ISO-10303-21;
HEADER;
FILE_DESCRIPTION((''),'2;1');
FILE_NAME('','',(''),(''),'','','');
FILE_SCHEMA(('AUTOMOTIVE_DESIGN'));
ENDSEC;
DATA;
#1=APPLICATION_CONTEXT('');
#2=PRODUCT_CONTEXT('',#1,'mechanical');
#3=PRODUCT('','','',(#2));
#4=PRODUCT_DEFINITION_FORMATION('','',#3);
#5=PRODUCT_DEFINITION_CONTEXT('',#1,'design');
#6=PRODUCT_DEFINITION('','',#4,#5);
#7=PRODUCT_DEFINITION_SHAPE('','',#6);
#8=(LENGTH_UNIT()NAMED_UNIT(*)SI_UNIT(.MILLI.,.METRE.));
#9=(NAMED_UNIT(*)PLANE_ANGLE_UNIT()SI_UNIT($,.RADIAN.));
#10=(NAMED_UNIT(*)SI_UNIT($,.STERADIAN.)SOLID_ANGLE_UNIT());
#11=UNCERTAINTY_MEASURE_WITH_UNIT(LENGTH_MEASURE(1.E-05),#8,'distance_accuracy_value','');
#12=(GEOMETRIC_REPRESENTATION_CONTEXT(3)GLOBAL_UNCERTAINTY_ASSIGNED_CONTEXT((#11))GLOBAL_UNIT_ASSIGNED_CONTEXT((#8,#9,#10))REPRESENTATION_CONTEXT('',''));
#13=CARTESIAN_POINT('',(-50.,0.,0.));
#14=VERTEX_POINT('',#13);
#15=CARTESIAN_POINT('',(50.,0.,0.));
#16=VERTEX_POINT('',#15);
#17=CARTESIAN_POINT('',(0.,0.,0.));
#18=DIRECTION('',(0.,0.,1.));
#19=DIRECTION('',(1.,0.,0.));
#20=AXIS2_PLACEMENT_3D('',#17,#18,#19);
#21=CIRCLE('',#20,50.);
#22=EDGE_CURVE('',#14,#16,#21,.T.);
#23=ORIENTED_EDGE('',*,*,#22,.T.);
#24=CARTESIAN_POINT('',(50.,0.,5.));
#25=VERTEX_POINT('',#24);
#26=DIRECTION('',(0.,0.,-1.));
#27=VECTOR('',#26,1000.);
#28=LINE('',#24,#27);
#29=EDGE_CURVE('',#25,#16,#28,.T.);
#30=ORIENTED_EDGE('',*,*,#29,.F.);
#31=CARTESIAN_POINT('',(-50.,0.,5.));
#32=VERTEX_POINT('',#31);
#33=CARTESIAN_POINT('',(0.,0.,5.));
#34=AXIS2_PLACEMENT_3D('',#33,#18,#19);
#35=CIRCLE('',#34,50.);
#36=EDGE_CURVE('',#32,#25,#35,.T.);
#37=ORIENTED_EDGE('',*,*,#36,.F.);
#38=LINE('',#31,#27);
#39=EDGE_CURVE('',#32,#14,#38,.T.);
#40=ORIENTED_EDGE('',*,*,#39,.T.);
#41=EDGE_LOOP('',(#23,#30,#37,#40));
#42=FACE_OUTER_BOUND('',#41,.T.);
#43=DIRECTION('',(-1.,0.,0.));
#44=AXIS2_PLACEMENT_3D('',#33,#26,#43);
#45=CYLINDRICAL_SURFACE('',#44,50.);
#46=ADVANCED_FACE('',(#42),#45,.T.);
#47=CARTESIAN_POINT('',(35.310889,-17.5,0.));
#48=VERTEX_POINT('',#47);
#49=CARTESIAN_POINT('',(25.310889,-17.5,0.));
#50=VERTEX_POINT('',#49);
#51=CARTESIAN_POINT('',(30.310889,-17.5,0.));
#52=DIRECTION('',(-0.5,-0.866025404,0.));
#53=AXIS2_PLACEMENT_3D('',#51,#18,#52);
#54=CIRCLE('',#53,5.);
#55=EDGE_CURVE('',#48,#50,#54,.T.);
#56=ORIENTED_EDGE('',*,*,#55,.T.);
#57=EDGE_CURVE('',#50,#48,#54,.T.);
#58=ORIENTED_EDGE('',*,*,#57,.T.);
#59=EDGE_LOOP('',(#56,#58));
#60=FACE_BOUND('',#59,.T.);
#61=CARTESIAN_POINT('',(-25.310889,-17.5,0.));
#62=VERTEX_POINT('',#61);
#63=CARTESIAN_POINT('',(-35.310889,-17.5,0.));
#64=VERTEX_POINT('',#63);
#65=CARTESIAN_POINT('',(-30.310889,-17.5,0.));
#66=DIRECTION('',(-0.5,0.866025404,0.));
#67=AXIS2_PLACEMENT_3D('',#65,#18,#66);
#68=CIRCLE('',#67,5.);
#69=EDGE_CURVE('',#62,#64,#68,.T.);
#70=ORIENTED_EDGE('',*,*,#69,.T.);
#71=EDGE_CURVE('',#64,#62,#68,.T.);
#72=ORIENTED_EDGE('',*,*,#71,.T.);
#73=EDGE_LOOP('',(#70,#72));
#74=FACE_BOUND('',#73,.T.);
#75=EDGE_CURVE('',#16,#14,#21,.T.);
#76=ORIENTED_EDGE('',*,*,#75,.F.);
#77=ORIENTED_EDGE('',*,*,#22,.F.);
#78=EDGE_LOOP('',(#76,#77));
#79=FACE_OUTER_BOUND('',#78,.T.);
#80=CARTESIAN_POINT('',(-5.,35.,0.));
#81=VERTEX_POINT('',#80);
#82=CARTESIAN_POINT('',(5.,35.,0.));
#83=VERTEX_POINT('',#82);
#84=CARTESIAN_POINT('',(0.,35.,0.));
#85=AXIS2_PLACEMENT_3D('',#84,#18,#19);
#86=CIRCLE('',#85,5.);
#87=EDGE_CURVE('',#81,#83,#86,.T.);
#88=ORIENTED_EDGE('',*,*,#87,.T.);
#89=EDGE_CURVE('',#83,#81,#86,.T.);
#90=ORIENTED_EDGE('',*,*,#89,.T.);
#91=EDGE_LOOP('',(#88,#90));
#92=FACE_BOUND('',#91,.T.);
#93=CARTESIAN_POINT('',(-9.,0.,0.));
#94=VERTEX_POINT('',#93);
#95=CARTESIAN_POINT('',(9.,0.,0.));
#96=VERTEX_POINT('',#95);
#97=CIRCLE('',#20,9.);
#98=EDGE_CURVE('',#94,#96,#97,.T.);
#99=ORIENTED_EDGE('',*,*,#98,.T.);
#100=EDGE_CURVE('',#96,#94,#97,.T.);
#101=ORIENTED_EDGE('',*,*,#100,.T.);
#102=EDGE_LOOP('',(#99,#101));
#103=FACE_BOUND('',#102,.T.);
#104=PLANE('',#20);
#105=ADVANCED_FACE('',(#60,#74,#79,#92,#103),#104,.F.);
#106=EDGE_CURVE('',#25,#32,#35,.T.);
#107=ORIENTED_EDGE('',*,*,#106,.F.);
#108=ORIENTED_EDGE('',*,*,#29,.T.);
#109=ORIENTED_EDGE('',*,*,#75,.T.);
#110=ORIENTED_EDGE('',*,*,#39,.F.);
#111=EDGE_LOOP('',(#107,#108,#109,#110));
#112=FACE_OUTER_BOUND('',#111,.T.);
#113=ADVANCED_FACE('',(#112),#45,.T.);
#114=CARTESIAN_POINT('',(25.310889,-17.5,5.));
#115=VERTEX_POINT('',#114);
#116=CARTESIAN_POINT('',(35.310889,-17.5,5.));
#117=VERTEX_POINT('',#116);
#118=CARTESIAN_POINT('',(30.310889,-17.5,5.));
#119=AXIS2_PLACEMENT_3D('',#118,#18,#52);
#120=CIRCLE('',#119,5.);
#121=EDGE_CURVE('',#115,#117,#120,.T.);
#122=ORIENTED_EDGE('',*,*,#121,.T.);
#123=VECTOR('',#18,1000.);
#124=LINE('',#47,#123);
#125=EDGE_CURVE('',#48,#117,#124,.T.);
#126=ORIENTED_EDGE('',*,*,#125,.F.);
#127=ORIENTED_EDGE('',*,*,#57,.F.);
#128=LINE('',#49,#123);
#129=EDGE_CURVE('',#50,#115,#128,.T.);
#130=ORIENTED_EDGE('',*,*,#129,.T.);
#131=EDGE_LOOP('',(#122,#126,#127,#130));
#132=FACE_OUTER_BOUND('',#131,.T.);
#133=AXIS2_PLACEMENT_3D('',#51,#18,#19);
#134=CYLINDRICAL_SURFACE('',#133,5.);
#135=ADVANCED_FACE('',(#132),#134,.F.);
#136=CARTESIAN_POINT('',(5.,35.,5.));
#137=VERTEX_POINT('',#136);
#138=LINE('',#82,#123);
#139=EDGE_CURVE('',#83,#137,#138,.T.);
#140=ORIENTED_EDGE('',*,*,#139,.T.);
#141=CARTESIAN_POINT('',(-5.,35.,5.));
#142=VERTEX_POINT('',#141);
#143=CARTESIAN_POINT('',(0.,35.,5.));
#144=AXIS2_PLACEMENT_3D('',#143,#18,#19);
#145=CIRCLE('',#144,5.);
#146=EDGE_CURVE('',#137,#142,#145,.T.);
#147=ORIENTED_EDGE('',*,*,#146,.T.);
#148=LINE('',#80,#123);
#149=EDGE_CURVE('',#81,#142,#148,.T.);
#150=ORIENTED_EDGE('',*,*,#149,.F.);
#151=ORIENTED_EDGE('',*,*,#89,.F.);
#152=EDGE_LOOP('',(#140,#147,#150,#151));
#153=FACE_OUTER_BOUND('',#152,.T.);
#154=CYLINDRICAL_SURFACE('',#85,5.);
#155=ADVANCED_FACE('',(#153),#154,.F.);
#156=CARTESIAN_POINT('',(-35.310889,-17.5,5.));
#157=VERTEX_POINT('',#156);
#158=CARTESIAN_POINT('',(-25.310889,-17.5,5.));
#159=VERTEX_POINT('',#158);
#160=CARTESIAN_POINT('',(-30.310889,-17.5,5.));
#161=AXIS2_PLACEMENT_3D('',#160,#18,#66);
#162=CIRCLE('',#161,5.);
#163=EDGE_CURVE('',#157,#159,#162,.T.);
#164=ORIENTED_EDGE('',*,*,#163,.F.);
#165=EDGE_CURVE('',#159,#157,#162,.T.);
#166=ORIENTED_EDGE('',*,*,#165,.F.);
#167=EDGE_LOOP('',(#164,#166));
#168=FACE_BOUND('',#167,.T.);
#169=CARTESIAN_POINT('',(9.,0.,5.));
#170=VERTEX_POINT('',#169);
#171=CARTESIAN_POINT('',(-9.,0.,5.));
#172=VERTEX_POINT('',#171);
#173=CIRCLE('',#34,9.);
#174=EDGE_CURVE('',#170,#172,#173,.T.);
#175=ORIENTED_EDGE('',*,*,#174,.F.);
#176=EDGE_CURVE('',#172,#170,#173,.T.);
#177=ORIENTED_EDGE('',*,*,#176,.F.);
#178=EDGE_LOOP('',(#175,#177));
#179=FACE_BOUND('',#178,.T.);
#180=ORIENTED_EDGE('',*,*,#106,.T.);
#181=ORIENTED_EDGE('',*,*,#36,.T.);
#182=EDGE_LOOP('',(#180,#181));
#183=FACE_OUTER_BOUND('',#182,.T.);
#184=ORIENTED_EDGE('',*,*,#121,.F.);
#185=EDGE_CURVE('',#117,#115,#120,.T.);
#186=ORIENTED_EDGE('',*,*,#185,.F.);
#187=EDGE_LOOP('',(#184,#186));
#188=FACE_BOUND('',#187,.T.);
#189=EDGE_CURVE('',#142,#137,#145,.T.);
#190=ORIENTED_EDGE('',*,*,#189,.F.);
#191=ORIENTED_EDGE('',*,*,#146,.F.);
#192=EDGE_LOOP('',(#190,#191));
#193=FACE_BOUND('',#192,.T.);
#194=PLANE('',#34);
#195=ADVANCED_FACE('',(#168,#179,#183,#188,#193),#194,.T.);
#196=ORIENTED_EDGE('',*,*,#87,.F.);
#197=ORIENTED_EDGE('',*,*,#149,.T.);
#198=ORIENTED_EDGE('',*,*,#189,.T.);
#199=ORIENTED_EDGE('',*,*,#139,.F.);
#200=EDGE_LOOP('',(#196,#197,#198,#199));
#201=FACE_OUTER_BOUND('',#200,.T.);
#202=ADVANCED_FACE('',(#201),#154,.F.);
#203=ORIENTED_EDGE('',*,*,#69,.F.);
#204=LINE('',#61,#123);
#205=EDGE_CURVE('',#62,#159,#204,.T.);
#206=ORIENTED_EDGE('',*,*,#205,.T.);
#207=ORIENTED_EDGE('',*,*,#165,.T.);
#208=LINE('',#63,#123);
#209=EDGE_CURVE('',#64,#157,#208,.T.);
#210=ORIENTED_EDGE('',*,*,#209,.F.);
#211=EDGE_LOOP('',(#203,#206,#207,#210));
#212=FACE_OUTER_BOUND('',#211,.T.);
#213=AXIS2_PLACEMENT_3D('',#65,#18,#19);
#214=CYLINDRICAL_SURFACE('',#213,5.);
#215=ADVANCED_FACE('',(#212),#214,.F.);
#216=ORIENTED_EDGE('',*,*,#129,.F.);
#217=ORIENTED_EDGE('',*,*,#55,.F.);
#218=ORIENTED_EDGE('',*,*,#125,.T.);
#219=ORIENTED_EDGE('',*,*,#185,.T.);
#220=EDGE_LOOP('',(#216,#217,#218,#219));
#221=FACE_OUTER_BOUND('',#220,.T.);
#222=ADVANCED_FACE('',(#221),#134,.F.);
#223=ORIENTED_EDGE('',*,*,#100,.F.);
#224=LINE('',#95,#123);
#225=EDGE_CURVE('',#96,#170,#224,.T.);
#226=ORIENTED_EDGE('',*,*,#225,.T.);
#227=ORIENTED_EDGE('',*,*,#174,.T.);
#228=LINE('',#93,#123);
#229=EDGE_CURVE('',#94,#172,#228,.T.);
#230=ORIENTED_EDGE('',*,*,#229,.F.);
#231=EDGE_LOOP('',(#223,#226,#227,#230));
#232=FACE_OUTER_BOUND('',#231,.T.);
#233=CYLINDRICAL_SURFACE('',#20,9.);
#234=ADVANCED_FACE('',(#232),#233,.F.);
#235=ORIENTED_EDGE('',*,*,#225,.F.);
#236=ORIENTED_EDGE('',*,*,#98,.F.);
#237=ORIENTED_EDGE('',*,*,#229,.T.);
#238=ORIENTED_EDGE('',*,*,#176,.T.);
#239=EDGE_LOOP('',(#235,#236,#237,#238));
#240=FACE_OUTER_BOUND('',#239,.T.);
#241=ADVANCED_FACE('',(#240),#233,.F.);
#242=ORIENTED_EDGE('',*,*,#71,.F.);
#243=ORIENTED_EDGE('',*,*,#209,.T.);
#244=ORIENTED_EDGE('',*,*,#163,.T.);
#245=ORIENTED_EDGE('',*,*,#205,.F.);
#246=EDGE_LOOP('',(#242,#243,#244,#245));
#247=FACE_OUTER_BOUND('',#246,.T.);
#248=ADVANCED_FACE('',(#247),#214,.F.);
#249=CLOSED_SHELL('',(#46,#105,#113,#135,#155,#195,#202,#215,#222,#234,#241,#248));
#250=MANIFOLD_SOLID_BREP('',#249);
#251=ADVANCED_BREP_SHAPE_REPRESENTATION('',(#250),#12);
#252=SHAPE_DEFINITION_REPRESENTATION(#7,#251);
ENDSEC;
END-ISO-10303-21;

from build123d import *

# Parameters (mm, degrees)
SKETCH1_R           = 50
BOSS_EXTRUDE1_DEPTH = 5
SKETCH2_R           = 5
CUT_EXTRUDE1_DEPTH  = 5
CIRPATTERN1_COUNT   = 3
SKETCH3_R           = 9
CUT_EXTRUDE2_DEPTH  = 5


with BuildPart() as part:
    # Sketch1 → Boss-Extrude1 (new body)
    with BuildSketch(Plane.XY):
        Circle(SKETCH1_R)
    extrude(amount=BOSS_EXTRUDE1_DEPTH)

    # Sketch2 → Cut-Extrude1 (cut)
    with BuildSketch(Plane.XY.offset(5)):
        with Locations((0, 35)):
            Circle(SKETCH2_R)
    cut_extrude1 = extrude(amount=-CUT_EXTRUDE1_DEPTH, mode=Mode.SUBTRACT)

    # CirPattern1: Cut-Extrude1 ×3 about axis
    cirpattern1_axis = Axis((0, 0, 0), (0, 0, 1))
    for i in range(1, CIRPATTERN1_COUNT):
        add(cut_extrude1.rotate(cirpattern1_axis, i * 360 / CIRPATTERN1_COUNT), mode=Mode.SUBTRACT)

    # Sketch3 → Cut-Extrude2 (cut)
    with BuildSketch(Plane.XY.offset(5)):
        Circle(SKETCH3_R)
    extrude(amount=-CUT_EXTRUDE2_DEPTH, mode=Mode.SUBTRACT)


solid = part.part
